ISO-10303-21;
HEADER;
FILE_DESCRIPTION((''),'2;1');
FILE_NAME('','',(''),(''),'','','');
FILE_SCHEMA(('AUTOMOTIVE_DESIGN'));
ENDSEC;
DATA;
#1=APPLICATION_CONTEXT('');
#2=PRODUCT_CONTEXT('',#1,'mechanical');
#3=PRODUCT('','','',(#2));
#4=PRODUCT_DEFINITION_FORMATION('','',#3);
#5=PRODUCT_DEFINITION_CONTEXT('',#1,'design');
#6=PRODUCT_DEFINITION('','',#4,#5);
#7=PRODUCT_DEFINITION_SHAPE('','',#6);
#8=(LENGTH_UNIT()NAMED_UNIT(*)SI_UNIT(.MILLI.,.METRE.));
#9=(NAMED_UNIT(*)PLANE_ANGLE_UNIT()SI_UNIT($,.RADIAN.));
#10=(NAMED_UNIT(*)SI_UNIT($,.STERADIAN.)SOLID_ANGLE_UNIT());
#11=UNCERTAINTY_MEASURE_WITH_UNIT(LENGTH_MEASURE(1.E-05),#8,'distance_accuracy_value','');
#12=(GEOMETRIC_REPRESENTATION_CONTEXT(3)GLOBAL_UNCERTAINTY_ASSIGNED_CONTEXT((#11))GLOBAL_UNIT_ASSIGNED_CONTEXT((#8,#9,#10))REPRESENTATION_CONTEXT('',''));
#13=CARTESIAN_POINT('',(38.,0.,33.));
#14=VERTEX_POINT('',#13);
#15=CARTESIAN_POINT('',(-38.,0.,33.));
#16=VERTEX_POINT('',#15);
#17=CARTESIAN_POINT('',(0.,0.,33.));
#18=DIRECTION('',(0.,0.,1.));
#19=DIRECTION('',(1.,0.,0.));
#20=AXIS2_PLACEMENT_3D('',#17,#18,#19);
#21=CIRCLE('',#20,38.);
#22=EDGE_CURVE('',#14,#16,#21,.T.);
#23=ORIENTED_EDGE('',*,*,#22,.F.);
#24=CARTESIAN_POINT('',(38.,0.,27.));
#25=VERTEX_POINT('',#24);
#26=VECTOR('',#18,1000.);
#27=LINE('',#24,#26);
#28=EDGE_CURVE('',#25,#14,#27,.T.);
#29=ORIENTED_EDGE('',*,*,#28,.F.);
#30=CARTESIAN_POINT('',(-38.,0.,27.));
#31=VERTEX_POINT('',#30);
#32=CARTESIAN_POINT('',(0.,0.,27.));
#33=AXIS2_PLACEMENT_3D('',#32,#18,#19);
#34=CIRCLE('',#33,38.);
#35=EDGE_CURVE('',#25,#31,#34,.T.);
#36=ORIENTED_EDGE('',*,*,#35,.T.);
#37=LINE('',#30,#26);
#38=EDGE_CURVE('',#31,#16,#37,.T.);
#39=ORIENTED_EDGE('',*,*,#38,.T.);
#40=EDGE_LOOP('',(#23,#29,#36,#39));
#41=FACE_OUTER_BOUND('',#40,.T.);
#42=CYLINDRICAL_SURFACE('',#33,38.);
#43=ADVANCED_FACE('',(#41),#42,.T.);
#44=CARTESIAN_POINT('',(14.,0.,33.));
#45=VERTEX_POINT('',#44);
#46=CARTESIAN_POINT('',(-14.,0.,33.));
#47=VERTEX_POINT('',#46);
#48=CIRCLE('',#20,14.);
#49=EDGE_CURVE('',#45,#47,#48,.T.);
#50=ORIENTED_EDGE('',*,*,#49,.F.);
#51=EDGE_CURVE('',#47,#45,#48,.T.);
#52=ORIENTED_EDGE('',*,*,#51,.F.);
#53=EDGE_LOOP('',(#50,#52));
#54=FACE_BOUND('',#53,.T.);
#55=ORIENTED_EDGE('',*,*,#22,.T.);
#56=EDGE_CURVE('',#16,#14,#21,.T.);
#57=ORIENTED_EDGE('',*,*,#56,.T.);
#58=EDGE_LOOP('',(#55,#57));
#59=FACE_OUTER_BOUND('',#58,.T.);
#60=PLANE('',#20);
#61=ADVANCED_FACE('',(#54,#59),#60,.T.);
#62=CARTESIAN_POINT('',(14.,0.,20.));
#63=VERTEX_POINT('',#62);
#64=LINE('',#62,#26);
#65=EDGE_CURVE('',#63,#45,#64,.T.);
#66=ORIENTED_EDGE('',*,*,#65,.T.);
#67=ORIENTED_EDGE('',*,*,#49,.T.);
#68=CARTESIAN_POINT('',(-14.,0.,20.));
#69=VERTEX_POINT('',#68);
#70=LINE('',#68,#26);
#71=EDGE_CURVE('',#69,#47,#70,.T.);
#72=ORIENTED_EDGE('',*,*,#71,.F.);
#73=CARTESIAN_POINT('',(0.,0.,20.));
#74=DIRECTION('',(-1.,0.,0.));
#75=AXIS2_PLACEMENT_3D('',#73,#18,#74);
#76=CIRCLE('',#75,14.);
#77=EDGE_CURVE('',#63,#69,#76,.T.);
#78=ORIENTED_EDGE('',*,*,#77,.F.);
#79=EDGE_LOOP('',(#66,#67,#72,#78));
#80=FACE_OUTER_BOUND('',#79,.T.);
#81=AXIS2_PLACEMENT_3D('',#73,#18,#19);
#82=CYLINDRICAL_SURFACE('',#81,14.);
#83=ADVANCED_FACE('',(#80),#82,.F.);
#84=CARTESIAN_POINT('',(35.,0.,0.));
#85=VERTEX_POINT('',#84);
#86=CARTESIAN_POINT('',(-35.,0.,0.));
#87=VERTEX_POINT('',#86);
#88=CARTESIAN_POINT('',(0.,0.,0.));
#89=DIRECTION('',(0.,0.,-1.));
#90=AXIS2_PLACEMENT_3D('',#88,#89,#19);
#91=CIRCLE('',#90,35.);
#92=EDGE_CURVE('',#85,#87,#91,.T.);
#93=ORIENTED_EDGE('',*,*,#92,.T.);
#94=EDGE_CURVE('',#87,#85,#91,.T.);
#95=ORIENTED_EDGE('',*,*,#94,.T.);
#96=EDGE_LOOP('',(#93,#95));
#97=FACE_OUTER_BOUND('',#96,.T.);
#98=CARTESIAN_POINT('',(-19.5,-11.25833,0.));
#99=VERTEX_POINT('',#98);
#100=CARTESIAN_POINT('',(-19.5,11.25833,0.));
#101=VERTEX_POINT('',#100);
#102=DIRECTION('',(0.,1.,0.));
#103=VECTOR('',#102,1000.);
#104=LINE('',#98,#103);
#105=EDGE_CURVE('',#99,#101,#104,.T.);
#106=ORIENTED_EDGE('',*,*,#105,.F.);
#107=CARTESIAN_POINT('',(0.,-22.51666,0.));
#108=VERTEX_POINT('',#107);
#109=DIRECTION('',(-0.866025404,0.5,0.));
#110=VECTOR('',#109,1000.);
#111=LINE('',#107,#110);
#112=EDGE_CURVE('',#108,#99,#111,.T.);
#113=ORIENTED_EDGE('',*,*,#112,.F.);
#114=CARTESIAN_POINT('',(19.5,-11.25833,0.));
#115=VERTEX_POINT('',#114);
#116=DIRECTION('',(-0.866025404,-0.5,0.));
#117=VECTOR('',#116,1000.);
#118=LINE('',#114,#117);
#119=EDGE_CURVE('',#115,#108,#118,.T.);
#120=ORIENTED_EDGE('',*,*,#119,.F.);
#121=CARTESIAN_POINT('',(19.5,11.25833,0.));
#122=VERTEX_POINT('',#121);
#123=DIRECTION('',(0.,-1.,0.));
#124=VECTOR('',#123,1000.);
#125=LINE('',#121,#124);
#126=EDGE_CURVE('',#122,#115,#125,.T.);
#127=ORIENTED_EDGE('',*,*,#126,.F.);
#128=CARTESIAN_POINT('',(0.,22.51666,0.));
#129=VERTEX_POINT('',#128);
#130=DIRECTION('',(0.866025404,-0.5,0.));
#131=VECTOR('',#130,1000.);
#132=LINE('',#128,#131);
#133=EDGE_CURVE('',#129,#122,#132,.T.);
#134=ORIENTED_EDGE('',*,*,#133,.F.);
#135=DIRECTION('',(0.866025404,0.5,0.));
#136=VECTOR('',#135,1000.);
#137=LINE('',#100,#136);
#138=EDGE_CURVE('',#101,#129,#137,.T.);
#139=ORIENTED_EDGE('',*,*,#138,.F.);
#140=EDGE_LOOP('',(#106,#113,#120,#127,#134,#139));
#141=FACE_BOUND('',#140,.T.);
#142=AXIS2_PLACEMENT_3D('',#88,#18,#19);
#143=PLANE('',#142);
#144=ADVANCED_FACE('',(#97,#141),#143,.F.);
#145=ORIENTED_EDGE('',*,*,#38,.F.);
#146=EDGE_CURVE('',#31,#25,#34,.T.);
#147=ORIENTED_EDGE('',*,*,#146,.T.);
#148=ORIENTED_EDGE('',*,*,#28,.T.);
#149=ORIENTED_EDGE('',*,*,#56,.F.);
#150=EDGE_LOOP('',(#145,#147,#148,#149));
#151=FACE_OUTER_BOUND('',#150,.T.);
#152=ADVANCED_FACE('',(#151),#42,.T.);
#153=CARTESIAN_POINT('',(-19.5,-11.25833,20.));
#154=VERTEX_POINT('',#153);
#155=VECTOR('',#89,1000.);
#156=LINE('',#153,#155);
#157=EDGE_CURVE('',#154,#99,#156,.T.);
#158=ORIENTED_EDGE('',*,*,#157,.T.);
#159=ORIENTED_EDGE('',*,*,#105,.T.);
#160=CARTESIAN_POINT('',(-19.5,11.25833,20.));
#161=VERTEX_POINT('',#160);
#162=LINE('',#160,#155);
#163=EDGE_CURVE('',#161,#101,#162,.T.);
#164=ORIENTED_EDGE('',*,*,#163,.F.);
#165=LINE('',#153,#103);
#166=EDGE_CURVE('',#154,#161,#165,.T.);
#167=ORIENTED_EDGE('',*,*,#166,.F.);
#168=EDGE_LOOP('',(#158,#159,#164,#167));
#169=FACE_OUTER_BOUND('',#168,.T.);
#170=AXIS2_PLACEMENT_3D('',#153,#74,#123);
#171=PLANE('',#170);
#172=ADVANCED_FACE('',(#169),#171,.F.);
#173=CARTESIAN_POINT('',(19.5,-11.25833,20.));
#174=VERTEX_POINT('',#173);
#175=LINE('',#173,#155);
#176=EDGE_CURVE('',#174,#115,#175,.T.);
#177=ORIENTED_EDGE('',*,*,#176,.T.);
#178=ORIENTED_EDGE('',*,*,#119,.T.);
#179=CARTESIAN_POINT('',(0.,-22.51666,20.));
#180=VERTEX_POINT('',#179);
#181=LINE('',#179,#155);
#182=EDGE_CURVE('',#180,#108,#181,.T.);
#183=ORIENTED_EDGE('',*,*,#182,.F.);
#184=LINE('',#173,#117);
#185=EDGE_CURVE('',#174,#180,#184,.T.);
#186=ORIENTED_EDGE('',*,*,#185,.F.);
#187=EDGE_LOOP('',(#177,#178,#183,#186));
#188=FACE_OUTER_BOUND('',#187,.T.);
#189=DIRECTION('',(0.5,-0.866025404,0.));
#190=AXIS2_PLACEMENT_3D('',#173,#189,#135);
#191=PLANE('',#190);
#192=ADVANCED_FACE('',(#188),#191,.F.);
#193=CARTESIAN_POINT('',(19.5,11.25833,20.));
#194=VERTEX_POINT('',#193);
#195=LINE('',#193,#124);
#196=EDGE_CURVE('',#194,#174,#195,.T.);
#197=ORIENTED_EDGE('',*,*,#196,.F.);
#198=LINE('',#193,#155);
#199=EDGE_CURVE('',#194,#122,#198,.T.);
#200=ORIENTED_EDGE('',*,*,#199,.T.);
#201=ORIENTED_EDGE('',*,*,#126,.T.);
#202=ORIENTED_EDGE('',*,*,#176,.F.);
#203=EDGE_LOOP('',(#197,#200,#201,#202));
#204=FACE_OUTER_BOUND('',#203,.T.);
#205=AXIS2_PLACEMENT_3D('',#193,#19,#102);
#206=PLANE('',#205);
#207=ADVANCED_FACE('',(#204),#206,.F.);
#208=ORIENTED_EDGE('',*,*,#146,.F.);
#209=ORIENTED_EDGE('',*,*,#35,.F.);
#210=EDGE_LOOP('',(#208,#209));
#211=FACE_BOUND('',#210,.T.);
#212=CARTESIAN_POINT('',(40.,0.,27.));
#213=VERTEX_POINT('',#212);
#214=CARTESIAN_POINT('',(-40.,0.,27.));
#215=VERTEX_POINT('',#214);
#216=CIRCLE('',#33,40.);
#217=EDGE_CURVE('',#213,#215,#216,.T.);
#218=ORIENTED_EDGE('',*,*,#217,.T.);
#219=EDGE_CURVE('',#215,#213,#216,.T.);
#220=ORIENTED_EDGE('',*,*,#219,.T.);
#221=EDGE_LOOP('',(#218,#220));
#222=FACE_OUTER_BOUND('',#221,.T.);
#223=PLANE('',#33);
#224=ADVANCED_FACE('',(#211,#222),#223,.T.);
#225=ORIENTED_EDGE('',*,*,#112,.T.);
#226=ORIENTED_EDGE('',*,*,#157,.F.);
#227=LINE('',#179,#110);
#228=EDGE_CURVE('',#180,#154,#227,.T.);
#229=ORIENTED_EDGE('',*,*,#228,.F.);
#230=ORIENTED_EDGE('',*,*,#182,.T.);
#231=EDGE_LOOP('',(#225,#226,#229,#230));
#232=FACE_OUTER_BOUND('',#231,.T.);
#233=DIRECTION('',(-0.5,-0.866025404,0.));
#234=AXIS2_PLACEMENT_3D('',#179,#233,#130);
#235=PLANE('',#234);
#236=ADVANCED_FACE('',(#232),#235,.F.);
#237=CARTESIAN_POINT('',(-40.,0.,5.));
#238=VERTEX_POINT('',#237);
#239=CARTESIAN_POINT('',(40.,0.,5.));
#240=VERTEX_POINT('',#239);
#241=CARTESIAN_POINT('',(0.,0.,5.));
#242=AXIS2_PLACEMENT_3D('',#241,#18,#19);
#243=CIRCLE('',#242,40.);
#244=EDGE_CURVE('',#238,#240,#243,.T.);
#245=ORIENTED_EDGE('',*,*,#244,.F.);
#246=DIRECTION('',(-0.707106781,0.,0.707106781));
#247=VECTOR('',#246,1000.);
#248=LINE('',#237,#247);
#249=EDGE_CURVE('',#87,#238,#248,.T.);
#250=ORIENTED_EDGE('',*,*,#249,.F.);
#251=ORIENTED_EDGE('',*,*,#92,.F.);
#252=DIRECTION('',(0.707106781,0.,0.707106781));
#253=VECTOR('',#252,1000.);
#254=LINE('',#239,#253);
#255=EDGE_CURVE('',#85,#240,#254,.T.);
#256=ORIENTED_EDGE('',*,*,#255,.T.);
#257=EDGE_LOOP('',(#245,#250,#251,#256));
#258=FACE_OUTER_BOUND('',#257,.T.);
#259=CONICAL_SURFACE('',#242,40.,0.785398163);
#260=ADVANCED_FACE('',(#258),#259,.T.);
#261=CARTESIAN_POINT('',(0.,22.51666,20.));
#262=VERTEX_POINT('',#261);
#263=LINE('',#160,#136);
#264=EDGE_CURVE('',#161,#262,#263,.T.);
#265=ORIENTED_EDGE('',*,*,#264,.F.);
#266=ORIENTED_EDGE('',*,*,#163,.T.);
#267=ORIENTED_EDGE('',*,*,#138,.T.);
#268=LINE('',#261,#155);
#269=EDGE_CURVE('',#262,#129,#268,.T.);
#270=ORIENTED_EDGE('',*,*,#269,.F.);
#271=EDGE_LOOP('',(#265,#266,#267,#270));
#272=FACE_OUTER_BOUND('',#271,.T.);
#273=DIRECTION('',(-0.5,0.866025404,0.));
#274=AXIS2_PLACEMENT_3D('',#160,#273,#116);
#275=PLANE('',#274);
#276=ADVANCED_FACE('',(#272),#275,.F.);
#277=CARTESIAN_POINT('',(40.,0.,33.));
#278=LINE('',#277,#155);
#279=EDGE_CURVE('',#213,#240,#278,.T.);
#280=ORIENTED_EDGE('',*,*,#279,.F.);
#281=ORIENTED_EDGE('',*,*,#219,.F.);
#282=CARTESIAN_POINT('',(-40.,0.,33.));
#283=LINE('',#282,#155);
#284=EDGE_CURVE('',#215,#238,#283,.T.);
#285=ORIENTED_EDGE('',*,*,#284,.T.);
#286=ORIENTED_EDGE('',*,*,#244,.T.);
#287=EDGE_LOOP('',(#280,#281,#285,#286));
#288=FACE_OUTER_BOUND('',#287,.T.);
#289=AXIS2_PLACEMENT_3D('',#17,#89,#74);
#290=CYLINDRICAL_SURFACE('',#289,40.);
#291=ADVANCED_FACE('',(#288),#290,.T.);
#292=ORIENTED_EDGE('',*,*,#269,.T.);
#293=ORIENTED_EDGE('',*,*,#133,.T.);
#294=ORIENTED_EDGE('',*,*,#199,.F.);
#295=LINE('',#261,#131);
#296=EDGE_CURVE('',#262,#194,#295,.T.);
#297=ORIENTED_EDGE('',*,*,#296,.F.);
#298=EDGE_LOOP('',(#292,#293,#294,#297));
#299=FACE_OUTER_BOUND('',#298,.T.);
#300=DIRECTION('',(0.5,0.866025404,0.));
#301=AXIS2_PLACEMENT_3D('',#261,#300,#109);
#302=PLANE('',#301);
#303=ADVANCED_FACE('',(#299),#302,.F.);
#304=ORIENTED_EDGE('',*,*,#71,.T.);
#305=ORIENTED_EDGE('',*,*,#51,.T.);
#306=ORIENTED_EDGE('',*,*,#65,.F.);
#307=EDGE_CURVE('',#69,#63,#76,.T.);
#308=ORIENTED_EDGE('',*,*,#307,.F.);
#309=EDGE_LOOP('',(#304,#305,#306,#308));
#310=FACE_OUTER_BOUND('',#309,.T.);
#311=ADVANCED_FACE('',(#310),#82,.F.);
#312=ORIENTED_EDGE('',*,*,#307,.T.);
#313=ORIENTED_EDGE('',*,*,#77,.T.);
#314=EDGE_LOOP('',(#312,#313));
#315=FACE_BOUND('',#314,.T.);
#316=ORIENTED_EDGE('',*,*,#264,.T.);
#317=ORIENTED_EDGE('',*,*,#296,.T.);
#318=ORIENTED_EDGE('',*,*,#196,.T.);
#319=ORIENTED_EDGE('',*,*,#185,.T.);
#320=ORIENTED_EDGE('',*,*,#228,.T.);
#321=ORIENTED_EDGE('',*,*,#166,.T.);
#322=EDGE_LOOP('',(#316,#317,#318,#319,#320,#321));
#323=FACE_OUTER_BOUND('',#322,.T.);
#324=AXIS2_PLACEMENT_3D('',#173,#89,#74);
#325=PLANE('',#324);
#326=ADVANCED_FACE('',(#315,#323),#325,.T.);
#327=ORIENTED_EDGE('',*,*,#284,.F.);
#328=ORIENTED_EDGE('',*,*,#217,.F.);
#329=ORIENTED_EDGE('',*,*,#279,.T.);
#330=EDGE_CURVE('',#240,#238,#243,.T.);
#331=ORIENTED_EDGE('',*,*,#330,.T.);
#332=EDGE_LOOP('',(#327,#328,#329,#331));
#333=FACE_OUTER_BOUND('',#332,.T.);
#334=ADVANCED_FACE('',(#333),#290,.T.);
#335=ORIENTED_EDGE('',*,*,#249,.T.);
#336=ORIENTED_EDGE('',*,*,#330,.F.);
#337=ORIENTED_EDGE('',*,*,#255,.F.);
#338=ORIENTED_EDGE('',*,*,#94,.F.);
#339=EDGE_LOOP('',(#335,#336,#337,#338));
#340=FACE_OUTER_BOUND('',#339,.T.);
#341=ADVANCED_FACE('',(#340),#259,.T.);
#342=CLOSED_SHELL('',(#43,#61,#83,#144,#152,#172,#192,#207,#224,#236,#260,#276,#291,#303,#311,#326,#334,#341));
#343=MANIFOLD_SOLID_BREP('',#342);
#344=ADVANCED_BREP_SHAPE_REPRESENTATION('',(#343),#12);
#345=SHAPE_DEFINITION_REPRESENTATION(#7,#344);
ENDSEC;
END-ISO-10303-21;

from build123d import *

# Parameters (mm, degrees)
SKETCH1_R           = 40
BOSS_EXTRUDE1_DEPTH = 33
CUT_EXTRUDE1_START  = -6
SKETCH2_R           = 40
SKETCH2_R_2         = 38
CUT_EXTRUDE1_DEPTH  = 6
CHAMFER1_SIZE       = 5
SKETCH3_R           = 14
CUT_EXTRUDE2_DEPTH  = 13
CUT_EXTRUDE3_DEPTH  = 20


with BuildPart() as part:
    # Sketch1 → Boss-Extrude1 (new body)
    with BuildSketch(Plane.XY):
        Circle(SKETCH1_R)
    extrude(amount=BOSS_EXTRUDE1_DEPTH)

    # Sketch2 → Cut-Extrude1 (cut)
    with BuildSketch(Plane.XY.offset(33).offset(CUT_EXTRUDE1_START)):
        Circle(SKETCH2_R)
        Circle(SKETCH2_R_2, mode=Mode.SUBTRACT)
    extrude(amount=CUT_EXTRUDE1_DEPTH, mode=Mode.SUBTRACT)

    # Chamfer1
    chamfer1_edges = [part.edges().sort_by_distance(p)[0] for p in [
        (-40, 0, 0),
    ]]
    chamfer(chamfer1_edges, length=CHAMFER1_SIZE)

    # Sketch3 → Cut-Extrude2 (cut)
    with BuildSketch(Plane.XY.offset(33)):
        Circle(SKETCH3_R)
    extrude(amount=-CUT_EXTRUDE2_DEPTH, mode=Mode.SUBTRACT)

    # Sketch4 → Cut-Extrude3 (cut)
    with BuildSketch(Plane(origin=(0, 0, 0), x_dir=(-1, 0, 0), z_dir=(0, 0, -1))):
        Polygon((-19.5, -11.258330249), (0, -22.516660498), (19.5, -11.258330249), (19.5, 11.258330249), (0, 22.516660498), (-19.5, 11.258330249), align=None)
    extrude(amount=-CUT_EXTRUDE3_DEPTH, mode=Mode.SUBTRACT)


solid = part.part
